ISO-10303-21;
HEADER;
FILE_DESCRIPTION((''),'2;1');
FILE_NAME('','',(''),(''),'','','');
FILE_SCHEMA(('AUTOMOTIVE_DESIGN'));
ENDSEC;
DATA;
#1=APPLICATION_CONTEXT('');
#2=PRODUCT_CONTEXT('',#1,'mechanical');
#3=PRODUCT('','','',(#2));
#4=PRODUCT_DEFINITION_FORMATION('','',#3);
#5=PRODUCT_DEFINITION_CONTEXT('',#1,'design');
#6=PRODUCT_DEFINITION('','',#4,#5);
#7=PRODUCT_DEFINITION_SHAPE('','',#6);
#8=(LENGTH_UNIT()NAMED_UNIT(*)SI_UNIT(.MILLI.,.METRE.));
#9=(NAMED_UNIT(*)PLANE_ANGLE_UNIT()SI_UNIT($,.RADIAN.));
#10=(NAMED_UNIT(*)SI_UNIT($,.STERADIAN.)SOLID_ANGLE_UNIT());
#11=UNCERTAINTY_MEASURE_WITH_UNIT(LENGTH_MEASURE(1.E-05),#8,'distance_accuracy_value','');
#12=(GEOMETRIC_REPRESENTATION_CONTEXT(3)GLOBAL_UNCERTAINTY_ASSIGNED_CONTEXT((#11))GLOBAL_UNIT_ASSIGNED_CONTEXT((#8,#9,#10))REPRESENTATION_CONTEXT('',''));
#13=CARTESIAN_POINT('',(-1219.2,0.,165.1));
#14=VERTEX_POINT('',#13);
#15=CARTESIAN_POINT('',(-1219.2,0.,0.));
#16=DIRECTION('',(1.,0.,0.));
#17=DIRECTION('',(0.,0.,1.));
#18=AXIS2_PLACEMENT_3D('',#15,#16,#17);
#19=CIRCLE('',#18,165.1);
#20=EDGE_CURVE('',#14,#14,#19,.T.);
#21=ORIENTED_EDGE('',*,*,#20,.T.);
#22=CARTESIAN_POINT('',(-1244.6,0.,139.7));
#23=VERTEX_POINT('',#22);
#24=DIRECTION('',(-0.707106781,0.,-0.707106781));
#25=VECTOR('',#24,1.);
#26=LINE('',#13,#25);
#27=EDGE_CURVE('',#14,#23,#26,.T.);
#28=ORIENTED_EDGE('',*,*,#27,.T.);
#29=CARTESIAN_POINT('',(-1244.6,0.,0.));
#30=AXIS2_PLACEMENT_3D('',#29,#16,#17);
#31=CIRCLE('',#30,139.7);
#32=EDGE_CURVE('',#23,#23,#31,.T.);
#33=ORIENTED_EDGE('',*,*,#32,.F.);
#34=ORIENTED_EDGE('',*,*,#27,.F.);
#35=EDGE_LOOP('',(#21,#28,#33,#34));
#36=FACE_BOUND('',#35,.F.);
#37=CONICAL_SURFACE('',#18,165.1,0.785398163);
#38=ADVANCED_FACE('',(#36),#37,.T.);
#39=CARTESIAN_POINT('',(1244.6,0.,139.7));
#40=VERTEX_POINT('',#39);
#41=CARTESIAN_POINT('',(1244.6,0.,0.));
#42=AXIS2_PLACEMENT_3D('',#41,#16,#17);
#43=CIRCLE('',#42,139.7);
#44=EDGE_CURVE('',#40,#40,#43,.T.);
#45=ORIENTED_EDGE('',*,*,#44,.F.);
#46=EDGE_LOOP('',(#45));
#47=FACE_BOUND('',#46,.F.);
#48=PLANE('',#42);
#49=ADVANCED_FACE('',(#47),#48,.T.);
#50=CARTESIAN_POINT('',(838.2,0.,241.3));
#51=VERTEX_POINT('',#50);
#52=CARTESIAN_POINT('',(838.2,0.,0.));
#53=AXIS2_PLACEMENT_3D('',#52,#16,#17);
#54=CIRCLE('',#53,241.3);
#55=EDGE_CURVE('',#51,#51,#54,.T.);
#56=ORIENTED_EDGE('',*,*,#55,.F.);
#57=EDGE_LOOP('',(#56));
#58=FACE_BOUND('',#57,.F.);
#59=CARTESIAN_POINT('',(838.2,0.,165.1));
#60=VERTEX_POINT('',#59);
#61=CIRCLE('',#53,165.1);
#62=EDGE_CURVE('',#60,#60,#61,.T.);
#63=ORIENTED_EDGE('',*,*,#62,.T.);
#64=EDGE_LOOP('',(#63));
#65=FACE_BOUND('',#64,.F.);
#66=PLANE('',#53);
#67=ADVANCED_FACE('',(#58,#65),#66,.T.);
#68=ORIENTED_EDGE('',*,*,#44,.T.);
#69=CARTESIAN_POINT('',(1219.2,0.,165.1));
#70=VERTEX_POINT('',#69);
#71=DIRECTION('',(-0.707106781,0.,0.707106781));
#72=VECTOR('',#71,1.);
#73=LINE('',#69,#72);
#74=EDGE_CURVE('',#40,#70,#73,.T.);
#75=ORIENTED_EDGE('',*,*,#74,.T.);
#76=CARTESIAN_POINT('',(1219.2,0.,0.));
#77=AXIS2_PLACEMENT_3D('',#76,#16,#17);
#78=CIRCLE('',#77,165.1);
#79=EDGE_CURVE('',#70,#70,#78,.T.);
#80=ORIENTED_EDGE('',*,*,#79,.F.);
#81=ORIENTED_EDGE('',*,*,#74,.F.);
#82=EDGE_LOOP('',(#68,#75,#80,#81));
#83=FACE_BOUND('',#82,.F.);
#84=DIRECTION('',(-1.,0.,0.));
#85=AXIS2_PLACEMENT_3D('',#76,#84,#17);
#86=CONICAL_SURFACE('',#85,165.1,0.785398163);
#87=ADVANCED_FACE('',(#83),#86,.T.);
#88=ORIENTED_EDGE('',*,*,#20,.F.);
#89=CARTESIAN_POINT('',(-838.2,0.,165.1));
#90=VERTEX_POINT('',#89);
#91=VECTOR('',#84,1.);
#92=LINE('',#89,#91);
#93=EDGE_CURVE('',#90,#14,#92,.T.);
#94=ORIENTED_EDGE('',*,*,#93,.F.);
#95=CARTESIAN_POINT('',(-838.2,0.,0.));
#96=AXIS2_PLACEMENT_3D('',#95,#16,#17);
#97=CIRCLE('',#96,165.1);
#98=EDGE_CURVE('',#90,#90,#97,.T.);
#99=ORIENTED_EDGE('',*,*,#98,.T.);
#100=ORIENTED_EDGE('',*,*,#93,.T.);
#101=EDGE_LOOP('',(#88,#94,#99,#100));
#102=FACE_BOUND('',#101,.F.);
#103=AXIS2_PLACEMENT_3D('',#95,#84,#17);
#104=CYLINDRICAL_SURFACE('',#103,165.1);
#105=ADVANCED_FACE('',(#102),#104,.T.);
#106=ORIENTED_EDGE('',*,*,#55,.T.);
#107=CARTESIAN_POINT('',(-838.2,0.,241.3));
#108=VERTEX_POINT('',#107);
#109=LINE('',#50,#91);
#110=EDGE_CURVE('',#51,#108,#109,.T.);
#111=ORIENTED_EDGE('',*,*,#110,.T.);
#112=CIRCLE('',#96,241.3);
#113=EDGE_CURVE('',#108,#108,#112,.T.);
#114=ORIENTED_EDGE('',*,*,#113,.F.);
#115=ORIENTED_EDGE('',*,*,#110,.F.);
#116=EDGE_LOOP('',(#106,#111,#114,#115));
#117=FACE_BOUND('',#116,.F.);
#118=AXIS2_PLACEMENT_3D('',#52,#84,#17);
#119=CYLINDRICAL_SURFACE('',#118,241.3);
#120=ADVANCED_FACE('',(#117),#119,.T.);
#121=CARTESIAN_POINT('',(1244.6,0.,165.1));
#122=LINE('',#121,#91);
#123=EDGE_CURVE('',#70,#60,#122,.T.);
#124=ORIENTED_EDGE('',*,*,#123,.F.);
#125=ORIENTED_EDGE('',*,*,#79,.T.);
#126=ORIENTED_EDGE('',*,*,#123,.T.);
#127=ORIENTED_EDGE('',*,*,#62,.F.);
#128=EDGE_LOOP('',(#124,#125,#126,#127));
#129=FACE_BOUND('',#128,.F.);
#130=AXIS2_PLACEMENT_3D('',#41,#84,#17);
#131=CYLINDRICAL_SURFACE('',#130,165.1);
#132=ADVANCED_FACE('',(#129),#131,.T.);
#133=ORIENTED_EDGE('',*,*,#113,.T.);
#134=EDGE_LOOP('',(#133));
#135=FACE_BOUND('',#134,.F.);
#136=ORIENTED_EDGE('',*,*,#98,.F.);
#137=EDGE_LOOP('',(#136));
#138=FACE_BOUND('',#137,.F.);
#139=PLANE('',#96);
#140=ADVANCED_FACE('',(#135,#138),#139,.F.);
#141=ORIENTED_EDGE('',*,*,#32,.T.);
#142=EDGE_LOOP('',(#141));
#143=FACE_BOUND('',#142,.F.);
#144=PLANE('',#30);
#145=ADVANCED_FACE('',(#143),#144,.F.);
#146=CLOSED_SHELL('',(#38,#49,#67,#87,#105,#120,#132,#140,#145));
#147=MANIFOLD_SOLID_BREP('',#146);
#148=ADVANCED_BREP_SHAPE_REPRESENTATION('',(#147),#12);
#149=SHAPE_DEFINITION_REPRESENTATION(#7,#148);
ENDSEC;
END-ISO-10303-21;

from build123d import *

# Parameters (mm, degrees)
CHAMFER1_SIZE = 25.4


with BuildPart() as part:
    # Sketch1 → Revolve1 (revolve)
    with BuildSketch(Plane.XY, mode=Mode.PRIVATE) as revolve1_sk:
        Polygon((-1244.6, 0), (1244.6, 0), (1244.6, 165.1), (838.2, 165.1), (838.2, 241.3), (-838.2, 241.3), (-838.2, 165.1), (-1244.6, 165.1), align=None)
    revolve(revolve1_sk.sketch.rotate(Axis((-1244.6, 0, 0), (1, 0, 0)), 90), axis=Axis((-1244.6, 0, 0), (1, 0, 0)))

    # Chamfer1
    chamfer1_edges = [part.edges().sort_by_distance(p)[0] for p in [
        (-1244.6, 0, -165.1),
        (1244.6, 0, -165.1),
    ]]
    chamfer(chamfer1_edges, length=CHAMFER1_SIZE)


solid = part.part
